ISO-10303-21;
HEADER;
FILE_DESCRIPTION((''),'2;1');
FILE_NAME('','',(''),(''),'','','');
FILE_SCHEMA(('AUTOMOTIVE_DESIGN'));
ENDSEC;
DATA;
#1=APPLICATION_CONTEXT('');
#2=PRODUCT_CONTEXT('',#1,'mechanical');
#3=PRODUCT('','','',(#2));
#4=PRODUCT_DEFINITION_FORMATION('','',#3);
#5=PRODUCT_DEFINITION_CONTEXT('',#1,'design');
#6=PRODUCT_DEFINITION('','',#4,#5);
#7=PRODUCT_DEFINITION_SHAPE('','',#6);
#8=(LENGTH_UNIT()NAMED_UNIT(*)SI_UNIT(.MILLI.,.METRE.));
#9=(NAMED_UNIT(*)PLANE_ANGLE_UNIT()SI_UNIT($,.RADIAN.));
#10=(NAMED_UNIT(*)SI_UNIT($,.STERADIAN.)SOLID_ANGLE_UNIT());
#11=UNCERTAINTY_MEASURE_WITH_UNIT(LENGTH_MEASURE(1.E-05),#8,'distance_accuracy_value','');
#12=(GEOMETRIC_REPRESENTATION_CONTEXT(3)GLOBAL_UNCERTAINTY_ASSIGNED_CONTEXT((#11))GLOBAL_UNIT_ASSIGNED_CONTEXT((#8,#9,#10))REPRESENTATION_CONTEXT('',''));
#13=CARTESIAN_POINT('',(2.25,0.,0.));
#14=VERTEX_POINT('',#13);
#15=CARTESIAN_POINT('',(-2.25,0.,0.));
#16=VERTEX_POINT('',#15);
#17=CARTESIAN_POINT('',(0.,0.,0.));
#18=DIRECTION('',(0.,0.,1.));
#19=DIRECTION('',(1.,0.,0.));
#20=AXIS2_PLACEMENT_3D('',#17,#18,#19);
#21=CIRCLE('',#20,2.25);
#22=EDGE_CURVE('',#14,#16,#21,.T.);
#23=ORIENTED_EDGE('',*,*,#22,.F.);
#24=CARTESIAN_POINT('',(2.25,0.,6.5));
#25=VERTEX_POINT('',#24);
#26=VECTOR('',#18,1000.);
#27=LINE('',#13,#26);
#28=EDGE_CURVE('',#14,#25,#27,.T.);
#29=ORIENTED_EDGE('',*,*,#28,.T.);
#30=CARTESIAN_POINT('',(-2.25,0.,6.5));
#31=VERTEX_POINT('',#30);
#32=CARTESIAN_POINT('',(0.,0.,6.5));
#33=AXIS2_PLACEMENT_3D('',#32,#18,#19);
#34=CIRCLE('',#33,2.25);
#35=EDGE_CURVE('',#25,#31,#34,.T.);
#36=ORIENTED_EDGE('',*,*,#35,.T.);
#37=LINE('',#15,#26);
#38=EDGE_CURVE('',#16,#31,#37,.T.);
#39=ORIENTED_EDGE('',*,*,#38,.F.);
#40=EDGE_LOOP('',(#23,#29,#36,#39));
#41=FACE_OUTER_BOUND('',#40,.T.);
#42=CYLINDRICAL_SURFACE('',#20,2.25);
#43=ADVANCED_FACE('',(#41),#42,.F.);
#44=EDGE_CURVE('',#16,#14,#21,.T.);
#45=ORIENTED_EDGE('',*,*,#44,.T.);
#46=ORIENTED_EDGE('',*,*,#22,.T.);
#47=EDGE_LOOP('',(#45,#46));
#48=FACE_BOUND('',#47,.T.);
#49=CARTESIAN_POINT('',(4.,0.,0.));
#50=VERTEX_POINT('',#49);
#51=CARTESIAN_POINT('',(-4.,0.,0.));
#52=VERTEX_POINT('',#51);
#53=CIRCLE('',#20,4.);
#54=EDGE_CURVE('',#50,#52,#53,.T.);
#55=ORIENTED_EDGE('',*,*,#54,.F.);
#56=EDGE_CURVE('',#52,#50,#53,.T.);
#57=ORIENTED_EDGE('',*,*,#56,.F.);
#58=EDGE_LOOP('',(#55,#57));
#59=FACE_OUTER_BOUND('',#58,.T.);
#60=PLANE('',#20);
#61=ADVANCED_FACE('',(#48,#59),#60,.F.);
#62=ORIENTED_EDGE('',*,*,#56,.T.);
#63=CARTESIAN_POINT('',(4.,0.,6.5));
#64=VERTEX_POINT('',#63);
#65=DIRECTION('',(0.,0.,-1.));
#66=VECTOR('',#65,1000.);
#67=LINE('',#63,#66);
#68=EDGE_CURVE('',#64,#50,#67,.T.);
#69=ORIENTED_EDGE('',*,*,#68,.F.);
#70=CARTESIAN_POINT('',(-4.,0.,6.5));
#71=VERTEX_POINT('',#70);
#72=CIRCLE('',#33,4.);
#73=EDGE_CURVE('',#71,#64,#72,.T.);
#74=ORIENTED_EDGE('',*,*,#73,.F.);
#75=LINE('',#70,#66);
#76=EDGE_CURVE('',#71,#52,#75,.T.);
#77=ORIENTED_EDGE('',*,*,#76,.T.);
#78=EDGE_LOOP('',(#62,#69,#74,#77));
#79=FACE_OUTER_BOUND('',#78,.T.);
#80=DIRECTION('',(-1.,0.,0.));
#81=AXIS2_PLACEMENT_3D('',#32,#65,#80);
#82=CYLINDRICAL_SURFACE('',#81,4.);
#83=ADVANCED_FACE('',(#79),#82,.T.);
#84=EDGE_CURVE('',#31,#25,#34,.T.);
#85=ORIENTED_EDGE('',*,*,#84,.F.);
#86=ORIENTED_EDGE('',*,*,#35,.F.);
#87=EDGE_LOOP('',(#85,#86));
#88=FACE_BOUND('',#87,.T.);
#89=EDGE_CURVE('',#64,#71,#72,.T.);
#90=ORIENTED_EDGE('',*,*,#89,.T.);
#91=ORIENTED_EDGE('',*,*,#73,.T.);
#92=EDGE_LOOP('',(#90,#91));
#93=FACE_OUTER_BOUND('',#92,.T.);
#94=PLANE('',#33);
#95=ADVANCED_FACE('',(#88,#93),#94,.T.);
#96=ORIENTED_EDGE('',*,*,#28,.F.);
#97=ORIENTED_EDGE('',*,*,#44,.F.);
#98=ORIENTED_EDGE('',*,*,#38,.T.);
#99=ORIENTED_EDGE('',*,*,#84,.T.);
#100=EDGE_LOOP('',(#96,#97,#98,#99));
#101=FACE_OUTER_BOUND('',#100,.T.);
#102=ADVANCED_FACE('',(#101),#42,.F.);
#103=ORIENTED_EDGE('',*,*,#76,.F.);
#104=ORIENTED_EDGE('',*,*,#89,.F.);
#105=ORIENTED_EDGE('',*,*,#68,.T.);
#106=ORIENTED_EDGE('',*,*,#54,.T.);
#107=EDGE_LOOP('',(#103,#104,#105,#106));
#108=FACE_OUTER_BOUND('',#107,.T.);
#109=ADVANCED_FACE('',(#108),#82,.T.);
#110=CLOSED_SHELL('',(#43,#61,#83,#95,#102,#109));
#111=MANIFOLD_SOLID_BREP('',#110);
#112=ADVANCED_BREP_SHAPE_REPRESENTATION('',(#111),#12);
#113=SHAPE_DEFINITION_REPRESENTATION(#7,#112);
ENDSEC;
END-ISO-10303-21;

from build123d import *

# Parameters (mm, degrees)
SKETCH_4_R          = 4
EXTRUDE_1_DEPTH     = 6.5
SKETCH_9_R          = 2.25
CUT_EXTRUDE_1_DEPTH = 9.61684397


with BuildPart() as part:
    # 草图4 → 凸台-拉伸1 (new body)
    with BuildSketch(Plane.XY):
        with Locations(Location((0, 0, 0), (0, 0, 180))):
            Circle(SKETCH_4_R)
    extrude(amount=EXTRUDE_1_DEPTH)

    # 草图9 → 切除-拉伸1 (cut, through all)
    with BuildSketch(Plane.XY.offset(6.5)):
        Circle(SKETCH_9_R)
    extrude(amount=-CUT_EXTRUDE_1_DEPTH, mode=Mode.SUBTRACT)


solid = part.part
